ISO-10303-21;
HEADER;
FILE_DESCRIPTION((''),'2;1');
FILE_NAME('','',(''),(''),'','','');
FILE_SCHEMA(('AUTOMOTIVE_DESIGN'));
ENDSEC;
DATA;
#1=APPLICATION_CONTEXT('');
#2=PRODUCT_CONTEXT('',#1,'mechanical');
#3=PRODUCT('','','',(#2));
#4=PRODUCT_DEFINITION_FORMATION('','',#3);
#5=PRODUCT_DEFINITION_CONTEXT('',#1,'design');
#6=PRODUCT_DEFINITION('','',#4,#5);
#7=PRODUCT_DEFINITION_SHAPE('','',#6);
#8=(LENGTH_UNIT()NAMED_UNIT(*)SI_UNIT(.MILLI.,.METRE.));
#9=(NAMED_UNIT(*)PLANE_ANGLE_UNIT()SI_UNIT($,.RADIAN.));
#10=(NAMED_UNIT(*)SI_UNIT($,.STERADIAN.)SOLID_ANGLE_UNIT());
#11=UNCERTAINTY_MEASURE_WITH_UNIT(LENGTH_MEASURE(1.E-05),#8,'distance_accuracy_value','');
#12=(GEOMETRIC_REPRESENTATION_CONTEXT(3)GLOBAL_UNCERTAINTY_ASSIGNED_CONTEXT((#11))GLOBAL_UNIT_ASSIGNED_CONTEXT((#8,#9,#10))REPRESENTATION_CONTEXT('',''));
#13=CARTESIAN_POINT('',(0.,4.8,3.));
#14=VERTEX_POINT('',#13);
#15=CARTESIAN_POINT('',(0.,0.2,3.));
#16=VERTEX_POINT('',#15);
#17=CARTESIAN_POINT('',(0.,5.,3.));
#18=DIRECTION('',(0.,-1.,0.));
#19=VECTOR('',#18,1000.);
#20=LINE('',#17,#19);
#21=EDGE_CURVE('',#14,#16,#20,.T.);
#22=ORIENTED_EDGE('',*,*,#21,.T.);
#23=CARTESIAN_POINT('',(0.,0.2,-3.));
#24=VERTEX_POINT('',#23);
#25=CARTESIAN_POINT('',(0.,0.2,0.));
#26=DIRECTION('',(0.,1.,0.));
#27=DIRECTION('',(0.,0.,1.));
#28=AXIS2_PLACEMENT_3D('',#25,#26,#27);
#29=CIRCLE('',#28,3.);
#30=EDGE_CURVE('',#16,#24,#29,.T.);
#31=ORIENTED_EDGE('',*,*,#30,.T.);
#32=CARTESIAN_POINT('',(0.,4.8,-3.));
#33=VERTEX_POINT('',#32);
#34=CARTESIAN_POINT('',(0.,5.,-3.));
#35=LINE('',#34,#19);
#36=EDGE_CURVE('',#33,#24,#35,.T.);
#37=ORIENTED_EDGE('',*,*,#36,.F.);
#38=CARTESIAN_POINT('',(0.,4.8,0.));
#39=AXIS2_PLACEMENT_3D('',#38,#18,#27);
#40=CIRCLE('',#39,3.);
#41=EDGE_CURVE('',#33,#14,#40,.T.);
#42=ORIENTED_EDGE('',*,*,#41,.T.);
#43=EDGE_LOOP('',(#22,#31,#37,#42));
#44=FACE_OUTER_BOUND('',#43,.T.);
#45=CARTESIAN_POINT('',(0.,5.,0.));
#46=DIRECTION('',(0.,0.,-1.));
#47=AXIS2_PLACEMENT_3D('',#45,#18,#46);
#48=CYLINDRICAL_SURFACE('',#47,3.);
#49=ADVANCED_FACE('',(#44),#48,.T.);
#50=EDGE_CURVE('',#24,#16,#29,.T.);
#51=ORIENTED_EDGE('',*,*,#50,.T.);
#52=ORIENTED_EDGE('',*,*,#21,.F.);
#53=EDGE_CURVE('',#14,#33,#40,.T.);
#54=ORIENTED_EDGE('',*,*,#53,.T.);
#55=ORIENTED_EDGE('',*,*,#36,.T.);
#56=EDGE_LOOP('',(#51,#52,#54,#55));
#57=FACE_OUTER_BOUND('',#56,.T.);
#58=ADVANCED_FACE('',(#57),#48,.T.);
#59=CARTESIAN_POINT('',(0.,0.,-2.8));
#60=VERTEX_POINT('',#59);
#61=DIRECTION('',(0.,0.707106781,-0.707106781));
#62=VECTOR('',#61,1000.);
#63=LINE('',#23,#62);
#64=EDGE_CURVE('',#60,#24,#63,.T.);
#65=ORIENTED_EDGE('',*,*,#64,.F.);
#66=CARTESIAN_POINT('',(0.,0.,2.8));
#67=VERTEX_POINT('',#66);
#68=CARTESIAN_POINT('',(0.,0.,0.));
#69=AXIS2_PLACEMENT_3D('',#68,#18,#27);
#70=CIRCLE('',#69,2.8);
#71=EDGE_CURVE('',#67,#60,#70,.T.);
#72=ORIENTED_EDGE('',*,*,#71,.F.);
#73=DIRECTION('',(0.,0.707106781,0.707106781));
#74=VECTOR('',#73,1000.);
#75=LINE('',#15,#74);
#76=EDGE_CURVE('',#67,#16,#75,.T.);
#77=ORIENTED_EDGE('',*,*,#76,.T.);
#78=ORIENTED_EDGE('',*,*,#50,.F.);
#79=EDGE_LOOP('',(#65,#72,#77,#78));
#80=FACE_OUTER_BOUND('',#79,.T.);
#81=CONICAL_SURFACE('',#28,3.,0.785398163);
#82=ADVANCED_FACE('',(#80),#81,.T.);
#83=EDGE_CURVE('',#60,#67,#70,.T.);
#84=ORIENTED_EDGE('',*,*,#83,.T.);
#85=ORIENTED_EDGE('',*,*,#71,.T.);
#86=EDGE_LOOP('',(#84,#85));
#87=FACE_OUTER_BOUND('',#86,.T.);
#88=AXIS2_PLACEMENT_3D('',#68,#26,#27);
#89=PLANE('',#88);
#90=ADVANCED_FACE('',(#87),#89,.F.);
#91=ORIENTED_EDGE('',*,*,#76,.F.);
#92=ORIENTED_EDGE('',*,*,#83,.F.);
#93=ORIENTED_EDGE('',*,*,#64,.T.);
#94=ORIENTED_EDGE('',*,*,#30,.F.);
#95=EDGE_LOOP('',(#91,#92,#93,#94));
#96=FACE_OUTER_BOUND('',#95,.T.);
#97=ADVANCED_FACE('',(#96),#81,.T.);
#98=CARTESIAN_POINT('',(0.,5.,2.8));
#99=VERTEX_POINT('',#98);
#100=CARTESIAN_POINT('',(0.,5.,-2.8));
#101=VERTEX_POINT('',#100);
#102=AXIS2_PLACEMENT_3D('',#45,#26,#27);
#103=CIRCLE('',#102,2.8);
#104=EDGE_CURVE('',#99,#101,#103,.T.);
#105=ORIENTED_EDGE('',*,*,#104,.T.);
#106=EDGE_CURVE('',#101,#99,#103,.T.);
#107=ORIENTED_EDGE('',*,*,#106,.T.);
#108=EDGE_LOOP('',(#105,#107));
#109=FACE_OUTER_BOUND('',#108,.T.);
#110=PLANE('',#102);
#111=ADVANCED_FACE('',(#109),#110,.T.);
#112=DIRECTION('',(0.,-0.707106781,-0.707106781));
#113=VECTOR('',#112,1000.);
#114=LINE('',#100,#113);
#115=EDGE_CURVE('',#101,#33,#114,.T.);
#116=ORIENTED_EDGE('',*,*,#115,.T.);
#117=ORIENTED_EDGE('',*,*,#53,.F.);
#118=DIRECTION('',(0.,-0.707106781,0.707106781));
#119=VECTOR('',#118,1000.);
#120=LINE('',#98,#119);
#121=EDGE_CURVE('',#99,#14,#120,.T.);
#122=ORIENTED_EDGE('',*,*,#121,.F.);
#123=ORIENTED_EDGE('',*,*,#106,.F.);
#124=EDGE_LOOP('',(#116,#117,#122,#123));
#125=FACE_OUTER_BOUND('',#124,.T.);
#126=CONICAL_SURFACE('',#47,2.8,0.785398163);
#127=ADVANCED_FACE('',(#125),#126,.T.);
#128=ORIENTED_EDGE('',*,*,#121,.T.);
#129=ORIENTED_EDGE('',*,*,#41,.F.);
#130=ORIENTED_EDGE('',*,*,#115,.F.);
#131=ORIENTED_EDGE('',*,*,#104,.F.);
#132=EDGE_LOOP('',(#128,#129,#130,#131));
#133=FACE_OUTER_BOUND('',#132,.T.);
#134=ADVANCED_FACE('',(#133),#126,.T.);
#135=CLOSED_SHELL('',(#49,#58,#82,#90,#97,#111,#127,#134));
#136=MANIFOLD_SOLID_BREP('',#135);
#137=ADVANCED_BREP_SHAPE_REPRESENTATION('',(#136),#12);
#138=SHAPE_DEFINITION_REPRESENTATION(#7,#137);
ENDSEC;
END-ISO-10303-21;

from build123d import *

# Parameters (mm, degrees)
SKETCH1_R           = 3
BOSS_EXTRUDE1_DEPTH = 5
CHAMFER1_SIZE       = 0.2


with BuildPart() as part:
    # Sketch1 → Boss-Extrude1 (new body)
    with BuildSketch(Plane(origin=(0, 0, 0), x_dir=(1, 0, 0), z_dir=(0, 1, 0))):
        with Locations(Location((0, 0, 0), (0, 0, 270))):
            Circle(SKETCH1_R)
    extrude(amount=BOSS_EXTRUDE1_DEPTH)

    # Chamfer1
    chamfer1_edges = [part.edges().sort_by_distance(p)[0] for p in [
        (0, 0, -3),
        (0, 5, -3),
    ]]
    chamfer(chamfer1_edges, length=CHAMFER1_SIZE)


solid = part.part
